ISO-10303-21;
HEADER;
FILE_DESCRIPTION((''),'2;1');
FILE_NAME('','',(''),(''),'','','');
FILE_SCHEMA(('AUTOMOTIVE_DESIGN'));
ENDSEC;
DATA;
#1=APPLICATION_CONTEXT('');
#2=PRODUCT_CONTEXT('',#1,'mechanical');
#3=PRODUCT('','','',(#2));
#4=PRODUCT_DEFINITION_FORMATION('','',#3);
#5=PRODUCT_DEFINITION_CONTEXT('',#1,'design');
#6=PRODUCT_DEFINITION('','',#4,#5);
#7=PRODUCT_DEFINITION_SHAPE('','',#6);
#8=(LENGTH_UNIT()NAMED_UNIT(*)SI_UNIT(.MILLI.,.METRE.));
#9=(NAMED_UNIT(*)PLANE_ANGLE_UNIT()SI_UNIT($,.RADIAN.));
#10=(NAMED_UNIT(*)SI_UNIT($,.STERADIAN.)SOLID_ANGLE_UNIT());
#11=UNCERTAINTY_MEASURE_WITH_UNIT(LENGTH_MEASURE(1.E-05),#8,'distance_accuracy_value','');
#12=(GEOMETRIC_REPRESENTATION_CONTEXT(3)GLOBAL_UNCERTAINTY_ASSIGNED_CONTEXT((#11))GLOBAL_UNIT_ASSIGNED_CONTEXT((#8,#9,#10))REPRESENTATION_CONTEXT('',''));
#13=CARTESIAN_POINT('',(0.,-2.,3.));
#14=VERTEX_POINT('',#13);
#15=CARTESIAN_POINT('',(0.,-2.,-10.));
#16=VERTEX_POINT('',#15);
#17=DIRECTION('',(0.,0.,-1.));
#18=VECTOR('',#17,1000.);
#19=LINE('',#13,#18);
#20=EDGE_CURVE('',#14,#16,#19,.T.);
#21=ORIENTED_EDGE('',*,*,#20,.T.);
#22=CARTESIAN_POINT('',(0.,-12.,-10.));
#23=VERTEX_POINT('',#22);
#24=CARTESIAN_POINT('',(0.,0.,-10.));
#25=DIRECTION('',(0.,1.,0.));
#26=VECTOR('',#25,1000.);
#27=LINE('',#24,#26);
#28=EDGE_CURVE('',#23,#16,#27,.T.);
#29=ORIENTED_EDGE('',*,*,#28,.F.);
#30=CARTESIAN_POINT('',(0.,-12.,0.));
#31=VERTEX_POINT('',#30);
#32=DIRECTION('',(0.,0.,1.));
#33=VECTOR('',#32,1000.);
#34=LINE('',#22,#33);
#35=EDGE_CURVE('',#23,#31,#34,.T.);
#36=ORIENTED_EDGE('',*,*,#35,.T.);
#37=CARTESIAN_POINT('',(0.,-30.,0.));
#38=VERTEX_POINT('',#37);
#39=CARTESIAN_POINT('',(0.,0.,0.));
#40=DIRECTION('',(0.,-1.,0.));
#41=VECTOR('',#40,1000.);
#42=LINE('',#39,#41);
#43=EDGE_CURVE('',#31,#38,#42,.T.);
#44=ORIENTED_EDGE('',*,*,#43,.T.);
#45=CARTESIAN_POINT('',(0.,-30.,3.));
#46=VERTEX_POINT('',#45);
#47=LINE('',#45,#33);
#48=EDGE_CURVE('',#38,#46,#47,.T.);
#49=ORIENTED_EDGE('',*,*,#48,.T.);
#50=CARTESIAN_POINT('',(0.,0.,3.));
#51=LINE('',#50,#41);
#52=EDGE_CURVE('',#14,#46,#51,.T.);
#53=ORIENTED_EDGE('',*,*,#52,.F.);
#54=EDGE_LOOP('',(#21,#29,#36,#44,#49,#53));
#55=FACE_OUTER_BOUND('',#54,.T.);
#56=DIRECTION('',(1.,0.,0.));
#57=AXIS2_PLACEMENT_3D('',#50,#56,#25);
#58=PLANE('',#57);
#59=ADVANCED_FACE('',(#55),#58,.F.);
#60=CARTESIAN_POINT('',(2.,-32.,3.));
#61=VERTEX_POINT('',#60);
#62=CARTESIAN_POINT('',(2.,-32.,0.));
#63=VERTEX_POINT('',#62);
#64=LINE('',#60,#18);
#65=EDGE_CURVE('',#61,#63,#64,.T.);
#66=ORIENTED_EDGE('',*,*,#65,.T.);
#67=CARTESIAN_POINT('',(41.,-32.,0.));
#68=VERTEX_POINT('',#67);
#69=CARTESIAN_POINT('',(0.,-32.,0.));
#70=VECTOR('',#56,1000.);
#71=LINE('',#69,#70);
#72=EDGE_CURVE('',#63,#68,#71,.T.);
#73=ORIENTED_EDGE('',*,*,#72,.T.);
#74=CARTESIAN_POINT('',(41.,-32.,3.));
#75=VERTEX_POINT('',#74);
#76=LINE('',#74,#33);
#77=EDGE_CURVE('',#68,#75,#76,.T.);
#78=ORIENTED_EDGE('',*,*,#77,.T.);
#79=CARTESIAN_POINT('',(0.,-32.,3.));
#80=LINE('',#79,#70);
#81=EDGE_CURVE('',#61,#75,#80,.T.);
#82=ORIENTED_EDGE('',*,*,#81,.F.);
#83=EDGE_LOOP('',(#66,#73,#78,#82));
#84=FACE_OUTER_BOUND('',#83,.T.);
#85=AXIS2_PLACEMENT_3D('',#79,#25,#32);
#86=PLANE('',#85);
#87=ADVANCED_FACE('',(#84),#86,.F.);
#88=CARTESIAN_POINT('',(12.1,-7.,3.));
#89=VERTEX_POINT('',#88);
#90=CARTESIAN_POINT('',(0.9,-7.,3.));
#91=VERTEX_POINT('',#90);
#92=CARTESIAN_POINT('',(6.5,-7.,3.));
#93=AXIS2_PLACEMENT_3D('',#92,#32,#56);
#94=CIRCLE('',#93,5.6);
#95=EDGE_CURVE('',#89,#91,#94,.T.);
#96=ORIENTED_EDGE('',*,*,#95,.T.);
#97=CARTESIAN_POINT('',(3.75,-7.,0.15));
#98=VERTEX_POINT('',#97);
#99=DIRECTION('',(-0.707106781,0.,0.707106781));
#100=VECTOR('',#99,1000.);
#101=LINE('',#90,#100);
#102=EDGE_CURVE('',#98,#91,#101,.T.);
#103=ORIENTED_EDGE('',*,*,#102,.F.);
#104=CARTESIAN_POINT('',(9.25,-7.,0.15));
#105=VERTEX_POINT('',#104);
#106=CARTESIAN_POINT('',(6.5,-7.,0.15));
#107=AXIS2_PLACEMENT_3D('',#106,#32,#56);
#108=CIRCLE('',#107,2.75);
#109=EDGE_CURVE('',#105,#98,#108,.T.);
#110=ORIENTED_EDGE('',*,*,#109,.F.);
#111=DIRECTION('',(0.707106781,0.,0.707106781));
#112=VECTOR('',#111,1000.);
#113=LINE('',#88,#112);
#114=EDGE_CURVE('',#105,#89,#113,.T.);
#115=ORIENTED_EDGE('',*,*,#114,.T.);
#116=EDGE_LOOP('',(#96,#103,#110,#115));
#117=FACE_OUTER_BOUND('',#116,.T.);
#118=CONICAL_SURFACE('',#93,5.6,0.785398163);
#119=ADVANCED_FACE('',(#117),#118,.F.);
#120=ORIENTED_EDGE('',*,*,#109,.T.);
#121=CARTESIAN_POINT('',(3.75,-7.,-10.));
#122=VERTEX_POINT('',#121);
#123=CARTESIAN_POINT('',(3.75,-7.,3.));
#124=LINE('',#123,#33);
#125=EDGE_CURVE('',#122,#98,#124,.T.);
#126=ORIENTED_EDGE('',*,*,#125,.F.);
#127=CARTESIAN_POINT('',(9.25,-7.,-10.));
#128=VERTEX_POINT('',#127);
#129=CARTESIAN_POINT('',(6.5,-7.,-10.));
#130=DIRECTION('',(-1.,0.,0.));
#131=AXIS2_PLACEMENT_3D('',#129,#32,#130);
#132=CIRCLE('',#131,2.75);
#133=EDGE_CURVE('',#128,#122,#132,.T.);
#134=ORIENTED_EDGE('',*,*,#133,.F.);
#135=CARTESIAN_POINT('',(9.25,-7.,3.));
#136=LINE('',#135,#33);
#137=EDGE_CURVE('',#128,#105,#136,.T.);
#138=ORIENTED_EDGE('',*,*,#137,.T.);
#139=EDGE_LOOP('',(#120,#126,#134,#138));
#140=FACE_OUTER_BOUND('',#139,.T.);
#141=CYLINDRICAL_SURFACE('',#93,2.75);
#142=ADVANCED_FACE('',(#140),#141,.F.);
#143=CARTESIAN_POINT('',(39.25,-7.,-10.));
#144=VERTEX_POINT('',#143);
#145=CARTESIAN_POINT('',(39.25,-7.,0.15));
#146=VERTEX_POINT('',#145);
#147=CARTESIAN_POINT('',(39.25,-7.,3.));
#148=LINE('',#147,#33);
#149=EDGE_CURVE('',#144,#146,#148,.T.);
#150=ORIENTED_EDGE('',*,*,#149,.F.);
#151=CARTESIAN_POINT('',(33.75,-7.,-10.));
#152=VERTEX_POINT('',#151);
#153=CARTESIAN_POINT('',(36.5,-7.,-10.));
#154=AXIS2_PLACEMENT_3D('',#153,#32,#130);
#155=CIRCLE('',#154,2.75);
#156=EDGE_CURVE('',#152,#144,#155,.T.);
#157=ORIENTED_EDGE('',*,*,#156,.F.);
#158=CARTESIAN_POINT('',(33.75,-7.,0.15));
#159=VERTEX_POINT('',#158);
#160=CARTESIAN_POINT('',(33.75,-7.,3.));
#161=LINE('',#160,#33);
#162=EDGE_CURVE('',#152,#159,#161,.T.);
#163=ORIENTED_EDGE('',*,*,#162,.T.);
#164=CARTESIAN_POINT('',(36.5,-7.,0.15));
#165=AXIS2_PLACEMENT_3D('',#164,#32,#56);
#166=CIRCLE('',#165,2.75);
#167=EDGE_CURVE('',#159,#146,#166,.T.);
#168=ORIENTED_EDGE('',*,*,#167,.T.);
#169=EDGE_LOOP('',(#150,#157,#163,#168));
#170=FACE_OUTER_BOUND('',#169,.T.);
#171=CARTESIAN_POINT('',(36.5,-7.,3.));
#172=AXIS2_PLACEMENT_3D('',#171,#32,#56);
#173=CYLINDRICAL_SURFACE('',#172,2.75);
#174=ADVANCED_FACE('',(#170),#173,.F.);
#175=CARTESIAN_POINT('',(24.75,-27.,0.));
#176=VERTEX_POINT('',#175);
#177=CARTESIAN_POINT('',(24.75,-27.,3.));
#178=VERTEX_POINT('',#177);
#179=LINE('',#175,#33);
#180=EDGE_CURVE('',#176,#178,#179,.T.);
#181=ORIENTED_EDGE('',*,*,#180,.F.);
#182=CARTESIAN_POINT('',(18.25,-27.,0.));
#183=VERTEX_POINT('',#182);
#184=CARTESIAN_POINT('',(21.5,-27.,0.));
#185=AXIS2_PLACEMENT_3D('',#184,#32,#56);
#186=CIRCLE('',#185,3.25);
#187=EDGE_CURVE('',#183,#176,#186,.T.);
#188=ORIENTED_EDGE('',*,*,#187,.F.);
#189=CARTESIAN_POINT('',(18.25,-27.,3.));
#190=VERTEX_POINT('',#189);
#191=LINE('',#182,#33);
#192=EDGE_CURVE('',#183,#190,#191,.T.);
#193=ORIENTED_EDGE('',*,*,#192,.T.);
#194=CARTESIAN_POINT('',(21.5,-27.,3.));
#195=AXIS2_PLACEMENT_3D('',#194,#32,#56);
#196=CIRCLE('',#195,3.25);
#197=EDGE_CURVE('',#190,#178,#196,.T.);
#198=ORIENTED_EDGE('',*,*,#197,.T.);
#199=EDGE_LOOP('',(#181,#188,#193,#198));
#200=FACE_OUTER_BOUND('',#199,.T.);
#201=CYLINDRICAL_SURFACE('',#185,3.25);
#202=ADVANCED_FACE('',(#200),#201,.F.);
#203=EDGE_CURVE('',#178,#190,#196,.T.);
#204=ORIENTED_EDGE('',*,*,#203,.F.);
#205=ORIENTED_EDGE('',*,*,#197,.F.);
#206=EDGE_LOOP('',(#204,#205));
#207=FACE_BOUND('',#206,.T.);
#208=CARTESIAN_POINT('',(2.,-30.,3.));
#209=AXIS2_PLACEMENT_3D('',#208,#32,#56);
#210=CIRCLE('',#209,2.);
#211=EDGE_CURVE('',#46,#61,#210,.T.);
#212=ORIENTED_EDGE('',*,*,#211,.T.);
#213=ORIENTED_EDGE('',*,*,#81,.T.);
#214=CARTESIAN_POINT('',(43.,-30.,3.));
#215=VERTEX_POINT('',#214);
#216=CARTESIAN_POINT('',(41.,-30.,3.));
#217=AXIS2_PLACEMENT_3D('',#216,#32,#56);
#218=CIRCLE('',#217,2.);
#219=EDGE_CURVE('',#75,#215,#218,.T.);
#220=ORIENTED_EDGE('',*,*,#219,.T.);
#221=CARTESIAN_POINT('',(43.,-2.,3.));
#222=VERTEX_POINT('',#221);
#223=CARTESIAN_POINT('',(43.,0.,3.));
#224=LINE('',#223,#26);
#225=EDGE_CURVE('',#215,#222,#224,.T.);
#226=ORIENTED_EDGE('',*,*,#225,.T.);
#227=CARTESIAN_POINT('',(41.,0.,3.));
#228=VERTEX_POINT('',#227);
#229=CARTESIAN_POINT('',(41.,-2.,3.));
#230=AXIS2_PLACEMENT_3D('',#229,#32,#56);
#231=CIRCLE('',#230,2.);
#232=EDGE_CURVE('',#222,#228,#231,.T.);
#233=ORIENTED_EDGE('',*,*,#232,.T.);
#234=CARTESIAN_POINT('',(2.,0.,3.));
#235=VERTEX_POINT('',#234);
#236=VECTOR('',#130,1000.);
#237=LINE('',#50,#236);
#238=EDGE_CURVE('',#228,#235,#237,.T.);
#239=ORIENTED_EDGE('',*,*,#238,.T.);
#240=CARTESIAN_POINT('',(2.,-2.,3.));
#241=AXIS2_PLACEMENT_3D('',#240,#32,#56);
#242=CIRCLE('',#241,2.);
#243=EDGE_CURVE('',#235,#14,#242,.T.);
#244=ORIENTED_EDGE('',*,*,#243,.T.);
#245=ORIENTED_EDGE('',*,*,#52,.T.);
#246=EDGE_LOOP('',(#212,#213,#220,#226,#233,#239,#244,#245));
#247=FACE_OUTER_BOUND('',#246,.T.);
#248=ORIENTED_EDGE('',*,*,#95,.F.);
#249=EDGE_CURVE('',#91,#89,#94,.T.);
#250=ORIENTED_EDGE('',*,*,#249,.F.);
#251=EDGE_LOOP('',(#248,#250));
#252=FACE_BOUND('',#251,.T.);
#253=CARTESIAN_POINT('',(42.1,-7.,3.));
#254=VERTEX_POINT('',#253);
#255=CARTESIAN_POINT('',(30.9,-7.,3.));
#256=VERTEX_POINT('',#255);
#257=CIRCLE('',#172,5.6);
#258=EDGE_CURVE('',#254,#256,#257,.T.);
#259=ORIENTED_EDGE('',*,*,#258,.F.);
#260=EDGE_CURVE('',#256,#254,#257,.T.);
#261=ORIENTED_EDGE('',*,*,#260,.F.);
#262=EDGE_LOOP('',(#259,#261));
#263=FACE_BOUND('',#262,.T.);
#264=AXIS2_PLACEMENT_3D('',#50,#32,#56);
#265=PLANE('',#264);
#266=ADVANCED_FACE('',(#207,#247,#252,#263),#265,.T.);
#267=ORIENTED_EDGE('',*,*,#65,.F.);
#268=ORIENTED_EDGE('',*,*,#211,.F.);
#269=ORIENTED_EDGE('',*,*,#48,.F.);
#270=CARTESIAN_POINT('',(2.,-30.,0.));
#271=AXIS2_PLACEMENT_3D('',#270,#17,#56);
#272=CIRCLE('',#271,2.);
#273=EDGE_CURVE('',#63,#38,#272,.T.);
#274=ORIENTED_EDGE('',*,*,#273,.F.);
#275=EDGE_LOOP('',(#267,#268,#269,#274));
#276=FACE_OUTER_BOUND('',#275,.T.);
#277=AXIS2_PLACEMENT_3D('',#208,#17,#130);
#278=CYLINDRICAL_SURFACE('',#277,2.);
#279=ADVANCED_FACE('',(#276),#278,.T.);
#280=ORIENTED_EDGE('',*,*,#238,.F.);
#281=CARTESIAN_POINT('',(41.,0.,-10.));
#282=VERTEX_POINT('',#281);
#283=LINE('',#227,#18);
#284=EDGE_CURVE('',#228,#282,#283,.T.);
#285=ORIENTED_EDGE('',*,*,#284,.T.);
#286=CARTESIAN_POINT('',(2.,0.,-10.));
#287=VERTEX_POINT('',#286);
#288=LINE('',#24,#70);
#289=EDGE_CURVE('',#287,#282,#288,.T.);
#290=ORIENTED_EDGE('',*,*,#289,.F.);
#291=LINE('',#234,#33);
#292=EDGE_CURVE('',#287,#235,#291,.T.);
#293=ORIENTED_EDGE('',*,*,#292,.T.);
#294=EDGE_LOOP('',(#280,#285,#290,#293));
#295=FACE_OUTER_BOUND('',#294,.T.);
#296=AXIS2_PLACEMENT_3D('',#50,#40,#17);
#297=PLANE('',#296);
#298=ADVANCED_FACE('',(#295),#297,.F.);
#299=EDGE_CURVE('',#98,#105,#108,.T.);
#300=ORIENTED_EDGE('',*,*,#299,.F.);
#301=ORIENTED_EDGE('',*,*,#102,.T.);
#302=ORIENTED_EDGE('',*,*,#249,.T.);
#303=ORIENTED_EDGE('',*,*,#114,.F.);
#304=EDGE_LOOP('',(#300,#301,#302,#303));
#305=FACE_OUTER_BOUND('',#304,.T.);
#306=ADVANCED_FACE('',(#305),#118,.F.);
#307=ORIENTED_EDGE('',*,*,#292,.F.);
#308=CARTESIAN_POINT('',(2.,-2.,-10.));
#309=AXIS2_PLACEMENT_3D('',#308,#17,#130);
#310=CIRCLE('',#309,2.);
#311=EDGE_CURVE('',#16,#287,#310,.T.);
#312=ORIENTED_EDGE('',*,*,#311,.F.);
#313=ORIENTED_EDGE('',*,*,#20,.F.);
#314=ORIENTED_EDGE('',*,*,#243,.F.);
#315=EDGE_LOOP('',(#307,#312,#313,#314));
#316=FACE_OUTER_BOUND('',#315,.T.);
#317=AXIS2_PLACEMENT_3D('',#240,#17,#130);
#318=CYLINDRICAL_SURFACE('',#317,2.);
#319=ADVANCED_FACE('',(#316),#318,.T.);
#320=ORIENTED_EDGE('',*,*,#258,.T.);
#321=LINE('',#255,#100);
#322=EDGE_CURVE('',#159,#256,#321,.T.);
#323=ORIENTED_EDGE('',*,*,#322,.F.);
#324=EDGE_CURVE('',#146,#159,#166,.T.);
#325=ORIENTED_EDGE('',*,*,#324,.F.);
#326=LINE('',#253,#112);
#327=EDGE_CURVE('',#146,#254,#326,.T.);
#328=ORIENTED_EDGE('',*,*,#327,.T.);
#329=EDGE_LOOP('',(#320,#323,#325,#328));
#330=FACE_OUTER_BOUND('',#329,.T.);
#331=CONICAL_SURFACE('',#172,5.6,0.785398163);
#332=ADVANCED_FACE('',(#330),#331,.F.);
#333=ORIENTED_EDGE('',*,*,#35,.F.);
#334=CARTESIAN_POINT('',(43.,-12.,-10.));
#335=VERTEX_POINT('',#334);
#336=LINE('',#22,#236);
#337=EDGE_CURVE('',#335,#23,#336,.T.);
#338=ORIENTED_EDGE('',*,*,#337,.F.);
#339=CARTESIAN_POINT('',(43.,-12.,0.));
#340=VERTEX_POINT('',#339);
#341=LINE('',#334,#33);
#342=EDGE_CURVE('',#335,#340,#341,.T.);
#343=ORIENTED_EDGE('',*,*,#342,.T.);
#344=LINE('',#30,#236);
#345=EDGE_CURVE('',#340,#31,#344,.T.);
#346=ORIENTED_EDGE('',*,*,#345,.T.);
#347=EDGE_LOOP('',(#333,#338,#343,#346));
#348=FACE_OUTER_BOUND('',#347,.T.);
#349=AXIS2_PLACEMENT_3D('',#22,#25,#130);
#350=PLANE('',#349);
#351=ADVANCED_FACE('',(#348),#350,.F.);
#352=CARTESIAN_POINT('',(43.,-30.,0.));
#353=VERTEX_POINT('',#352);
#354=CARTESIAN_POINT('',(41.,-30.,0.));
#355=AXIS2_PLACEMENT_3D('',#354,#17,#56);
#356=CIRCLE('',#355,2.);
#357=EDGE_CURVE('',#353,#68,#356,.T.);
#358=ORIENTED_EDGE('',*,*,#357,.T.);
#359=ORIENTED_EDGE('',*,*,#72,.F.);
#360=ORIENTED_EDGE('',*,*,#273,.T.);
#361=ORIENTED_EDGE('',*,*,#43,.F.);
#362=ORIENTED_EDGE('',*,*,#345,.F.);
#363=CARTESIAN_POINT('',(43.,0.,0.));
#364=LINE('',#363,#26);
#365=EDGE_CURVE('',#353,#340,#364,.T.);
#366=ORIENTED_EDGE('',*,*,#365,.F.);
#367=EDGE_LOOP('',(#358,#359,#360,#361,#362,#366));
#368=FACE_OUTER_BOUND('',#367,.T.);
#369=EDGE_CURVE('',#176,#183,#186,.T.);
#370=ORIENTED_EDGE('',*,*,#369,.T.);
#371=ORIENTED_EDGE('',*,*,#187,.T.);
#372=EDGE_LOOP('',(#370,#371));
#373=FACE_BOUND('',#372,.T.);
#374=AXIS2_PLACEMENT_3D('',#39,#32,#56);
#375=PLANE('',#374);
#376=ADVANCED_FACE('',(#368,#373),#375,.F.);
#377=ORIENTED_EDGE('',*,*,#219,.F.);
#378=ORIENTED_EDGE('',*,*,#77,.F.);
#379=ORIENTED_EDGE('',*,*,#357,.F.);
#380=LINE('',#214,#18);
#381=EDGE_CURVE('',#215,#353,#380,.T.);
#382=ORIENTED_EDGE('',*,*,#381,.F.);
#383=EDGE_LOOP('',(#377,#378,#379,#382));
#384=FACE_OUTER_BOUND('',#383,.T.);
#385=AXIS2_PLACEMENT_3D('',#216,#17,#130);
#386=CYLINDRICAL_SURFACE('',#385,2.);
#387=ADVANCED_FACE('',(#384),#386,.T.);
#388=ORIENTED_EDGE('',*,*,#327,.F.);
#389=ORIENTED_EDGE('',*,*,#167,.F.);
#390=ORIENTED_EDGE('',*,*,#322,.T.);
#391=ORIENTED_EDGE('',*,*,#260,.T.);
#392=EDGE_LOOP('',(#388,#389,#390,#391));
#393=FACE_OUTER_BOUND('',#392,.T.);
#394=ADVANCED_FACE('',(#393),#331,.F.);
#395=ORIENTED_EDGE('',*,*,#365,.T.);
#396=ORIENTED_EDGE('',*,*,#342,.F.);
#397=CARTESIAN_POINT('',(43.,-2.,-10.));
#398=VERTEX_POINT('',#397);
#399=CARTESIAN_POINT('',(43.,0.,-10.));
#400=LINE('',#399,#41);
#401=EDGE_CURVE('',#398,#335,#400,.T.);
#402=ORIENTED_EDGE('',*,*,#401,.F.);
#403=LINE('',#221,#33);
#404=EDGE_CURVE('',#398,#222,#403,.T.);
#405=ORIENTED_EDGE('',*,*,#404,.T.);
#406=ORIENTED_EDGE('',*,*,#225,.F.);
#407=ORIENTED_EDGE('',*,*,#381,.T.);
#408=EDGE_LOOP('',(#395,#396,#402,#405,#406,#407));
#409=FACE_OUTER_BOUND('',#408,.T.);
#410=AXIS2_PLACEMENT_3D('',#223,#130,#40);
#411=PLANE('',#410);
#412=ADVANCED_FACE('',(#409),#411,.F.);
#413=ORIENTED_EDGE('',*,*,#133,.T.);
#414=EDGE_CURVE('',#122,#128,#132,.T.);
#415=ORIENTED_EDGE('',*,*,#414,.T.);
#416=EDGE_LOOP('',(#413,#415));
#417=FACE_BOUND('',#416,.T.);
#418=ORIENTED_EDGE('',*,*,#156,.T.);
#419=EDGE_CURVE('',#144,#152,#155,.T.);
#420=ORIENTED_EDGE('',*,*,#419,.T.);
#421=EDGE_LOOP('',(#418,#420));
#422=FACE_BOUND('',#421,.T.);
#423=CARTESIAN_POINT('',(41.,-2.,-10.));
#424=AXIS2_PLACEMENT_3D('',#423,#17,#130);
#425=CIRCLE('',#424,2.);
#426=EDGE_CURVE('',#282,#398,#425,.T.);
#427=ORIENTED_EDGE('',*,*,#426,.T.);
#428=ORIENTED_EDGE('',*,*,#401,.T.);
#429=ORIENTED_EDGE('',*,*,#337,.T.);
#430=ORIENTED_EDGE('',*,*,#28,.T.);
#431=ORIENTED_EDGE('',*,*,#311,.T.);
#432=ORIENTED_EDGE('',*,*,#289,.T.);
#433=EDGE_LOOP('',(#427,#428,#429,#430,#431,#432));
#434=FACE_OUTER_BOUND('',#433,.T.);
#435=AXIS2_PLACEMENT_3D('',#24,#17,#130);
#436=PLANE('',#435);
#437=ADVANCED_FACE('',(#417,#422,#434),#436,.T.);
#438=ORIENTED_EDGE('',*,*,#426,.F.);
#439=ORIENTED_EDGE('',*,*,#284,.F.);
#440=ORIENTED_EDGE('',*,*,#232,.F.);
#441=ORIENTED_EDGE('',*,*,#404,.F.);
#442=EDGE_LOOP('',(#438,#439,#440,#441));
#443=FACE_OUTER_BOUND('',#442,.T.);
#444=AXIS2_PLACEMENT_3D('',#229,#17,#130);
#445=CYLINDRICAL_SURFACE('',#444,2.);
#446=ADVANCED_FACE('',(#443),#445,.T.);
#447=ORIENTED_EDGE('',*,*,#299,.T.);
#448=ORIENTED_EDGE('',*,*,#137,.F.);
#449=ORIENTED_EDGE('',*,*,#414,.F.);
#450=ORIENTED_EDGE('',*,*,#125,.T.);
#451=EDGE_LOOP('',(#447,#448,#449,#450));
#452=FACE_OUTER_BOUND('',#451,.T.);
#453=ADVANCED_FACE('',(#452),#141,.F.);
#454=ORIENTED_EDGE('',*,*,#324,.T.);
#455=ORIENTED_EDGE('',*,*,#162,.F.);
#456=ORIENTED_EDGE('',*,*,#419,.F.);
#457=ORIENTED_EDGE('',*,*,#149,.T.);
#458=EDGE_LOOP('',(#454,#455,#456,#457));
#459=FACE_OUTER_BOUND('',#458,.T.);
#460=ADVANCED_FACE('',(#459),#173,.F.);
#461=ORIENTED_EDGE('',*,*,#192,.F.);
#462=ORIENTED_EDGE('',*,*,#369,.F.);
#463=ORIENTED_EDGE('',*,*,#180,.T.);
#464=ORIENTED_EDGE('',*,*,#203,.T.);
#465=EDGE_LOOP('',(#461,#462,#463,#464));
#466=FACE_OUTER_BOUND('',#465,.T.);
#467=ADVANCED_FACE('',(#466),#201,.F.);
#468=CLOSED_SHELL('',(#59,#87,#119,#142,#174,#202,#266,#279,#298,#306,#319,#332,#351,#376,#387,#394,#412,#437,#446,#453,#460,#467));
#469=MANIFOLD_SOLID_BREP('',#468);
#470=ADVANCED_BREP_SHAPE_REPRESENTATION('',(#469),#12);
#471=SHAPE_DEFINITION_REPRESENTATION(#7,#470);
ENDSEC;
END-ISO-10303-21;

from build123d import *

# Parameters (mm, degrees)
SKETCH_1_W                  = 43
SKETCH_1_H                  = 32
EXTRUDE_1_DEPTH             = 3
HOLE_WIZARD_M5_1_AT_2_COUNT = 2
HOLE_WIZARD_M5_1_AT_2_PITCH = 30
SKETCH_4_R                  = 3.25
CUT_EXTRUDE_1_DEPTH         = 3
FILLET_1_R                  = 2
SKETCH_5_R                  = 2.75
EXTRUDE_2_DEPTH             = 10


with BuildPart() as part:
    # 草图1 → 凸台-拉伸1 (new body)
    with BuildSketch(Plane.XY):
        with Locations((21.5, -16)):
            Rectangle(SKETCH_1_W, SKETCH_1_H)
    extrude(amount=EXTRUDE_1_DEPTH)

    # 草图2 → M5 六角凹锥坑螺钉的锥形沉头孔1 (revolve, cut)
    with BuildSketch(Plane(origin=(6.5, -7, 3), x_dir=(0, -1, 0), z_dir=(1, 0, 0))):
        Polygon((0, 0), (0, 3), (2.75, 3), (2.75, 2.85), (5.6, 0), align=None)
    hole_wizard_m5_1 = revolve(axis=Axis((6.5, -7, 9.35), (0, 0, -1)), mode=Mode.SUBTRACT)

    # M5 六角凹锥坑螺钉的锥形沉头孔1 at 2: M5 六角凹锥坑螺钉的锥形沉头孔1 ×2
    with Locations(*[(i * HOLE_WIZARD_M5_1_AT_2_PITCH, 0, 0) for i in range(1, HOLE_WIZARD_M5_1_AT_2_COUNT)]):
        add(hole_wizard_m5_1, mode=Mode.SUBTRACT)

    # 草图4 → 切除-拉伸1 (cut)
    with BuildSketch(Plane.XY.offset(3)):
        with Locations((21.5, -27)):
            Circle(SKETCH_4_R)
    extrude(amount=-CUT_EXTRUDE_1_DEPTH, mode=Mode.SUBTRACT)

    # 圆角1
    fillet_1_edges = [part.edges().sort_by_distance(p)[0] for p in [
        (0, 0, 1.5),
        (43, 0, 1.5),
        (43, -32, 1.5),
        (0, -32, 1.5),
    ]]
    fillet(fillet_1_edges, radius=FILLET_1_R)

    # 草图5 → 凸台-拉伸2 (add)
    with BuildSketch(Plane(origin=(0, 0, 0), x_dir=(-1, 0, 0), z_dir=(0, 0, -1))):
        with BuildLine():
            Line((-43, -2), (-43, -12))
            Line((-43, -12), (0, -12))
            Line((0, -12), (0, -2))
            ThreePointArc((0, -2), (-0.585786438, -0.585786438), (-2, 0))
            Line((-2, 0), (-41, 0))
            ThreePointArc((-41, 0), (-42.414213562, -0.585786438), (-43, -2))
        make_face()
        with Locations(Location((-36.5, -7, 0), (0, 0, 180))):
            Circle(SKETCH_5_R, mode=Mode.SUBTRACT)
        with Locations(Location((-6.5, -7, 0), (0, 0, 180))):
            Circle(SKETCH_5_R, mode=Mode.SUBTRACT)
    extrude(amount=EXTRUDE_2_DEPTH)


solid = part.part
